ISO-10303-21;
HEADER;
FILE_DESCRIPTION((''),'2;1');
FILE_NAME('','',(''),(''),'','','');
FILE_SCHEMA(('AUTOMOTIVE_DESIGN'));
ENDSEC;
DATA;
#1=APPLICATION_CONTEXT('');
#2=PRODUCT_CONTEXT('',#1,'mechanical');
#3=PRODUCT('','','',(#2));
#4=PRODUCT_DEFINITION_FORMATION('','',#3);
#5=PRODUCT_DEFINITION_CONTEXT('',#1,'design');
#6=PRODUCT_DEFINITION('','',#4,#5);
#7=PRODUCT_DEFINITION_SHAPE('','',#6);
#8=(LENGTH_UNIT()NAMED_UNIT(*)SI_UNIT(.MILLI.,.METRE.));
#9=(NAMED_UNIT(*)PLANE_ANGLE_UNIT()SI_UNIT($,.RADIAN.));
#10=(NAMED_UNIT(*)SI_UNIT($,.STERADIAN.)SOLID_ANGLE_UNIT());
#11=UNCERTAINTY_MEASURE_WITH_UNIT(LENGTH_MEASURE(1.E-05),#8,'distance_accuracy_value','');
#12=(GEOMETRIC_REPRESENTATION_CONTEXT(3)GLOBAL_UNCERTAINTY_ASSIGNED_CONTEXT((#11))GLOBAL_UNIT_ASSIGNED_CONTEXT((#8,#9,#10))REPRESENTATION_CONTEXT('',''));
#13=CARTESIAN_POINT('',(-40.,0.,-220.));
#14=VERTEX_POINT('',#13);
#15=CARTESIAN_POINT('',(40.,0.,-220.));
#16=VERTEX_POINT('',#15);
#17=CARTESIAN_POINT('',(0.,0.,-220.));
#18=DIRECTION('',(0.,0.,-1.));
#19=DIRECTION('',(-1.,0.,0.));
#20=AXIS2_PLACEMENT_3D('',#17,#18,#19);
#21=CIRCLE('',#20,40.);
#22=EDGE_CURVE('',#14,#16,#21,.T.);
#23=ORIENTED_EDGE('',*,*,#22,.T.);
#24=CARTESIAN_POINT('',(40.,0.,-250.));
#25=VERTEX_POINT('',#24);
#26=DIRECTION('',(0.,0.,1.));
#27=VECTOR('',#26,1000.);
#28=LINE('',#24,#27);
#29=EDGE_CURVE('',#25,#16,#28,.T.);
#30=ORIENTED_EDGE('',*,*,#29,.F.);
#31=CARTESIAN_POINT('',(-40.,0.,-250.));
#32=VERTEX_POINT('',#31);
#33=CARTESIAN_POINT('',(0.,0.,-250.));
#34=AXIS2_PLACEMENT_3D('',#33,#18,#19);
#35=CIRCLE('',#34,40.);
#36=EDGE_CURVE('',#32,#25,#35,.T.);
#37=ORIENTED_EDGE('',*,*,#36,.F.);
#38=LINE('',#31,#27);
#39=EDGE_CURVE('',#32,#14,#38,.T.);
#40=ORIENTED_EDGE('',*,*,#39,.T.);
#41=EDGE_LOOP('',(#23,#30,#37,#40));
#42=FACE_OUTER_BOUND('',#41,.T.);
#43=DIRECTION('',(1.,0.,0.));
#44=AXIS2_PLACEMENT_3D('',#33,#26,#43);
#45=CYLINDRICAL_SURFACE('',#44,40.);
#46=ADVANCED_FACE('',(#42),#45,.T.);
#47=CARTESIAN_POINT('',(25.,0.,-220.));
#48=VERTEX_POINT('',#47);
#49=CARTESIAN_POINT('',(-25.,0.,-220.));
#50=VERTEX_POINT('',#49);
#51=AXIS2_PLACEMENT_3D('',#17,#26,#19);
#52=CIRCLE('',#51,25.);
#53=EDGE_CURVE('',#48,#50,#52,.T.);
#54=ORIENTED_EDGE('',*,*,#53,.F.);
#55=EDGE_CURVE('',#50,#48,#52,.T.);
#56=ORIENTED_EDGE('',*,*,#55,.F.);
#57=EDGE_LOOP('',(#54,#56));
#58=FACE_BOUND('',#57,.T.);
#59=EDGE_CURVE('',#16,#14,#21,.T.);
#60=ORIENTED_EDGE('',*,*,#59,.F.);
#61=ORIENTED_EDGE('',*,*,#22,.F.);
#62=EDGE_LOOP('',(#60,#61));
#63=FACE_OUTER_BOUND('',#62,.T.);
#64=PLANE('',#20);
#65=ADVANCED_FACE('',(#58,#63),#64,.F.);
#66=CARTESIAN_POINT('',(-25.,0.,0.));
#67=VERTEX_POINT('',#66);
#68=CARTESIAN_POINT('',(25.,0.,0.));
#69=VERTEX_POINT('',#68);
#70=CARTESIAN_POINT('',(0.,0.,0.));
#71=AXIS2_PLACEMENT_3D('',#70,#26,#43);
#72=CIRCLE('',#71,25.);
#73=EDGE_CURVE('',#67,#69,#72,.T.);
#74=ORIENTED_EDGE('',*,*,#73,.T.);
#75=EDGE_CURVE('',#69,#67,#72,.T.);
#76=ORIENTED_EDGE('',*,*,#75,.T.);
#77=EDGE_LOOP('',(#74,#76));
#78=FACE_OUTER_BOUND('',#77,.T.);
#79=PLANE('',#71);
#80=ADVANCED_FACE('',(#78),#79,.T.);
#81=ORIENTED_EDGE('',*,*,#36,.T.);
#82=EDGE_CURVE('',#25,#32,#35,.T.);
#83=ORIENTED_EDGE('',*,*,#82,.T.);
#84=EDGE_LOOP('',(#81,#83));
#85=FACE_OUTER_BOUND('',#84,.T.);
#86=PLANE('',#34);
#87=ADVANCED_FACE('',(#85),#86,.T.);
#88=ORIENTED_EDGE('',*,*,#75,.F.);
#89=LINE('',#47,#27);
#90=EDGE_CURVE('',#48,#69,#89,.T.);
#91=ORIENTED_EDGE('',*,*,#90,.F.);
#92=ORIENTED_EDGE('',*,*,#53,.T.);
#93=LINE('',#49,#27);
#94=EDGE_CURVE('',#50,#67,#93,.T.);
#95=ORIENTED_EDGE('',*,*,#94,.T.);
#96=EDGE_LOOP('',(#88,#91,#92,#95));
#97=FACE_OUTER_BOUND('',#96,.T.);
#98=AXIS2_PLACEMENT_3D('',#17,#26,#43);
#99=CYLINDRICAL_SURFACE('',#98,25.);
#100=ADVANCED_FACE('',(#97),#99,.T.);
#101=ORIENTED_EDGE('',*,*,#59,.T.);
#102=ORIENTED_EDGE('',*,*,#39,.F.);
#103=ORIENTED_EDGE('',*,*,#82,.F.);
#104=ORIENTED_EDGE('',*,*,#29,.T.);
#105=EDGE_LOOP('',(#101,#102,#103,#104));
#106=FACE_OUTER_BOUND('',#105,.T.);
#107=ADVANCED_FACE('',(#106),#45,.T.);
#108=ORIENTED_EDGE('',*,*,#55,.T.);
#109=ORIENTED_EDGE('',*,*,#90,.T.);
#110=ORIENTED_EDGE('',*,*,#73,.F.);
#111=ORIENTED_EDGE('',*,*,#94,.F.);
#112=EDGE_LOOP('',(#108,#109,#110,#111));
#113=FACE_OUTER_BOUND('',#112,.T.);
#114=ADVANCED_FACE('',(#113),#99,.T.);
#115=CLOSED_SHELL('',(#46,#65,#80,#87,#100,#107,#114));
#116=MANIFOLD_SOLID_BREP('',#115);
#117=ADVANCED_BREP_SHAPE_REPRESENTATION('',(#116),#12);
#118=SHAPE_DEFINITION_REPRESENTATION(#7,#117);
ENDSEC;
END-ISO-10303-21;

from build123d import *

# Parameters (mm, degrees)
SKETCH1_R           = 25
BOSS_EXTRUDE1_DEPTH = 220
SKETCH2_R           = 40
BOSS_EXTRUDE2_DEPTH = 30


with BuildPart() as part:
    # Sketch1 → Boss-Extrude1 (new body)
    with BuildSketch(Plane.XY):
        Circle(SKETCH1_R)
    extrude(amount=-BOSS_EXTRUDE1_DEPTH)

    # Sketch2 → Boss-Extrude2 (add)
    with BuildSketch(Plane(origin=(0, 0, -220), x_dir=(-1, 0, 0), z_dir=(0, 0, -1))):
        Circle(SKETCH2_R)
    extrude(amount=BOSS_EXTRUDE2_DEPTH)


solid = part.part
